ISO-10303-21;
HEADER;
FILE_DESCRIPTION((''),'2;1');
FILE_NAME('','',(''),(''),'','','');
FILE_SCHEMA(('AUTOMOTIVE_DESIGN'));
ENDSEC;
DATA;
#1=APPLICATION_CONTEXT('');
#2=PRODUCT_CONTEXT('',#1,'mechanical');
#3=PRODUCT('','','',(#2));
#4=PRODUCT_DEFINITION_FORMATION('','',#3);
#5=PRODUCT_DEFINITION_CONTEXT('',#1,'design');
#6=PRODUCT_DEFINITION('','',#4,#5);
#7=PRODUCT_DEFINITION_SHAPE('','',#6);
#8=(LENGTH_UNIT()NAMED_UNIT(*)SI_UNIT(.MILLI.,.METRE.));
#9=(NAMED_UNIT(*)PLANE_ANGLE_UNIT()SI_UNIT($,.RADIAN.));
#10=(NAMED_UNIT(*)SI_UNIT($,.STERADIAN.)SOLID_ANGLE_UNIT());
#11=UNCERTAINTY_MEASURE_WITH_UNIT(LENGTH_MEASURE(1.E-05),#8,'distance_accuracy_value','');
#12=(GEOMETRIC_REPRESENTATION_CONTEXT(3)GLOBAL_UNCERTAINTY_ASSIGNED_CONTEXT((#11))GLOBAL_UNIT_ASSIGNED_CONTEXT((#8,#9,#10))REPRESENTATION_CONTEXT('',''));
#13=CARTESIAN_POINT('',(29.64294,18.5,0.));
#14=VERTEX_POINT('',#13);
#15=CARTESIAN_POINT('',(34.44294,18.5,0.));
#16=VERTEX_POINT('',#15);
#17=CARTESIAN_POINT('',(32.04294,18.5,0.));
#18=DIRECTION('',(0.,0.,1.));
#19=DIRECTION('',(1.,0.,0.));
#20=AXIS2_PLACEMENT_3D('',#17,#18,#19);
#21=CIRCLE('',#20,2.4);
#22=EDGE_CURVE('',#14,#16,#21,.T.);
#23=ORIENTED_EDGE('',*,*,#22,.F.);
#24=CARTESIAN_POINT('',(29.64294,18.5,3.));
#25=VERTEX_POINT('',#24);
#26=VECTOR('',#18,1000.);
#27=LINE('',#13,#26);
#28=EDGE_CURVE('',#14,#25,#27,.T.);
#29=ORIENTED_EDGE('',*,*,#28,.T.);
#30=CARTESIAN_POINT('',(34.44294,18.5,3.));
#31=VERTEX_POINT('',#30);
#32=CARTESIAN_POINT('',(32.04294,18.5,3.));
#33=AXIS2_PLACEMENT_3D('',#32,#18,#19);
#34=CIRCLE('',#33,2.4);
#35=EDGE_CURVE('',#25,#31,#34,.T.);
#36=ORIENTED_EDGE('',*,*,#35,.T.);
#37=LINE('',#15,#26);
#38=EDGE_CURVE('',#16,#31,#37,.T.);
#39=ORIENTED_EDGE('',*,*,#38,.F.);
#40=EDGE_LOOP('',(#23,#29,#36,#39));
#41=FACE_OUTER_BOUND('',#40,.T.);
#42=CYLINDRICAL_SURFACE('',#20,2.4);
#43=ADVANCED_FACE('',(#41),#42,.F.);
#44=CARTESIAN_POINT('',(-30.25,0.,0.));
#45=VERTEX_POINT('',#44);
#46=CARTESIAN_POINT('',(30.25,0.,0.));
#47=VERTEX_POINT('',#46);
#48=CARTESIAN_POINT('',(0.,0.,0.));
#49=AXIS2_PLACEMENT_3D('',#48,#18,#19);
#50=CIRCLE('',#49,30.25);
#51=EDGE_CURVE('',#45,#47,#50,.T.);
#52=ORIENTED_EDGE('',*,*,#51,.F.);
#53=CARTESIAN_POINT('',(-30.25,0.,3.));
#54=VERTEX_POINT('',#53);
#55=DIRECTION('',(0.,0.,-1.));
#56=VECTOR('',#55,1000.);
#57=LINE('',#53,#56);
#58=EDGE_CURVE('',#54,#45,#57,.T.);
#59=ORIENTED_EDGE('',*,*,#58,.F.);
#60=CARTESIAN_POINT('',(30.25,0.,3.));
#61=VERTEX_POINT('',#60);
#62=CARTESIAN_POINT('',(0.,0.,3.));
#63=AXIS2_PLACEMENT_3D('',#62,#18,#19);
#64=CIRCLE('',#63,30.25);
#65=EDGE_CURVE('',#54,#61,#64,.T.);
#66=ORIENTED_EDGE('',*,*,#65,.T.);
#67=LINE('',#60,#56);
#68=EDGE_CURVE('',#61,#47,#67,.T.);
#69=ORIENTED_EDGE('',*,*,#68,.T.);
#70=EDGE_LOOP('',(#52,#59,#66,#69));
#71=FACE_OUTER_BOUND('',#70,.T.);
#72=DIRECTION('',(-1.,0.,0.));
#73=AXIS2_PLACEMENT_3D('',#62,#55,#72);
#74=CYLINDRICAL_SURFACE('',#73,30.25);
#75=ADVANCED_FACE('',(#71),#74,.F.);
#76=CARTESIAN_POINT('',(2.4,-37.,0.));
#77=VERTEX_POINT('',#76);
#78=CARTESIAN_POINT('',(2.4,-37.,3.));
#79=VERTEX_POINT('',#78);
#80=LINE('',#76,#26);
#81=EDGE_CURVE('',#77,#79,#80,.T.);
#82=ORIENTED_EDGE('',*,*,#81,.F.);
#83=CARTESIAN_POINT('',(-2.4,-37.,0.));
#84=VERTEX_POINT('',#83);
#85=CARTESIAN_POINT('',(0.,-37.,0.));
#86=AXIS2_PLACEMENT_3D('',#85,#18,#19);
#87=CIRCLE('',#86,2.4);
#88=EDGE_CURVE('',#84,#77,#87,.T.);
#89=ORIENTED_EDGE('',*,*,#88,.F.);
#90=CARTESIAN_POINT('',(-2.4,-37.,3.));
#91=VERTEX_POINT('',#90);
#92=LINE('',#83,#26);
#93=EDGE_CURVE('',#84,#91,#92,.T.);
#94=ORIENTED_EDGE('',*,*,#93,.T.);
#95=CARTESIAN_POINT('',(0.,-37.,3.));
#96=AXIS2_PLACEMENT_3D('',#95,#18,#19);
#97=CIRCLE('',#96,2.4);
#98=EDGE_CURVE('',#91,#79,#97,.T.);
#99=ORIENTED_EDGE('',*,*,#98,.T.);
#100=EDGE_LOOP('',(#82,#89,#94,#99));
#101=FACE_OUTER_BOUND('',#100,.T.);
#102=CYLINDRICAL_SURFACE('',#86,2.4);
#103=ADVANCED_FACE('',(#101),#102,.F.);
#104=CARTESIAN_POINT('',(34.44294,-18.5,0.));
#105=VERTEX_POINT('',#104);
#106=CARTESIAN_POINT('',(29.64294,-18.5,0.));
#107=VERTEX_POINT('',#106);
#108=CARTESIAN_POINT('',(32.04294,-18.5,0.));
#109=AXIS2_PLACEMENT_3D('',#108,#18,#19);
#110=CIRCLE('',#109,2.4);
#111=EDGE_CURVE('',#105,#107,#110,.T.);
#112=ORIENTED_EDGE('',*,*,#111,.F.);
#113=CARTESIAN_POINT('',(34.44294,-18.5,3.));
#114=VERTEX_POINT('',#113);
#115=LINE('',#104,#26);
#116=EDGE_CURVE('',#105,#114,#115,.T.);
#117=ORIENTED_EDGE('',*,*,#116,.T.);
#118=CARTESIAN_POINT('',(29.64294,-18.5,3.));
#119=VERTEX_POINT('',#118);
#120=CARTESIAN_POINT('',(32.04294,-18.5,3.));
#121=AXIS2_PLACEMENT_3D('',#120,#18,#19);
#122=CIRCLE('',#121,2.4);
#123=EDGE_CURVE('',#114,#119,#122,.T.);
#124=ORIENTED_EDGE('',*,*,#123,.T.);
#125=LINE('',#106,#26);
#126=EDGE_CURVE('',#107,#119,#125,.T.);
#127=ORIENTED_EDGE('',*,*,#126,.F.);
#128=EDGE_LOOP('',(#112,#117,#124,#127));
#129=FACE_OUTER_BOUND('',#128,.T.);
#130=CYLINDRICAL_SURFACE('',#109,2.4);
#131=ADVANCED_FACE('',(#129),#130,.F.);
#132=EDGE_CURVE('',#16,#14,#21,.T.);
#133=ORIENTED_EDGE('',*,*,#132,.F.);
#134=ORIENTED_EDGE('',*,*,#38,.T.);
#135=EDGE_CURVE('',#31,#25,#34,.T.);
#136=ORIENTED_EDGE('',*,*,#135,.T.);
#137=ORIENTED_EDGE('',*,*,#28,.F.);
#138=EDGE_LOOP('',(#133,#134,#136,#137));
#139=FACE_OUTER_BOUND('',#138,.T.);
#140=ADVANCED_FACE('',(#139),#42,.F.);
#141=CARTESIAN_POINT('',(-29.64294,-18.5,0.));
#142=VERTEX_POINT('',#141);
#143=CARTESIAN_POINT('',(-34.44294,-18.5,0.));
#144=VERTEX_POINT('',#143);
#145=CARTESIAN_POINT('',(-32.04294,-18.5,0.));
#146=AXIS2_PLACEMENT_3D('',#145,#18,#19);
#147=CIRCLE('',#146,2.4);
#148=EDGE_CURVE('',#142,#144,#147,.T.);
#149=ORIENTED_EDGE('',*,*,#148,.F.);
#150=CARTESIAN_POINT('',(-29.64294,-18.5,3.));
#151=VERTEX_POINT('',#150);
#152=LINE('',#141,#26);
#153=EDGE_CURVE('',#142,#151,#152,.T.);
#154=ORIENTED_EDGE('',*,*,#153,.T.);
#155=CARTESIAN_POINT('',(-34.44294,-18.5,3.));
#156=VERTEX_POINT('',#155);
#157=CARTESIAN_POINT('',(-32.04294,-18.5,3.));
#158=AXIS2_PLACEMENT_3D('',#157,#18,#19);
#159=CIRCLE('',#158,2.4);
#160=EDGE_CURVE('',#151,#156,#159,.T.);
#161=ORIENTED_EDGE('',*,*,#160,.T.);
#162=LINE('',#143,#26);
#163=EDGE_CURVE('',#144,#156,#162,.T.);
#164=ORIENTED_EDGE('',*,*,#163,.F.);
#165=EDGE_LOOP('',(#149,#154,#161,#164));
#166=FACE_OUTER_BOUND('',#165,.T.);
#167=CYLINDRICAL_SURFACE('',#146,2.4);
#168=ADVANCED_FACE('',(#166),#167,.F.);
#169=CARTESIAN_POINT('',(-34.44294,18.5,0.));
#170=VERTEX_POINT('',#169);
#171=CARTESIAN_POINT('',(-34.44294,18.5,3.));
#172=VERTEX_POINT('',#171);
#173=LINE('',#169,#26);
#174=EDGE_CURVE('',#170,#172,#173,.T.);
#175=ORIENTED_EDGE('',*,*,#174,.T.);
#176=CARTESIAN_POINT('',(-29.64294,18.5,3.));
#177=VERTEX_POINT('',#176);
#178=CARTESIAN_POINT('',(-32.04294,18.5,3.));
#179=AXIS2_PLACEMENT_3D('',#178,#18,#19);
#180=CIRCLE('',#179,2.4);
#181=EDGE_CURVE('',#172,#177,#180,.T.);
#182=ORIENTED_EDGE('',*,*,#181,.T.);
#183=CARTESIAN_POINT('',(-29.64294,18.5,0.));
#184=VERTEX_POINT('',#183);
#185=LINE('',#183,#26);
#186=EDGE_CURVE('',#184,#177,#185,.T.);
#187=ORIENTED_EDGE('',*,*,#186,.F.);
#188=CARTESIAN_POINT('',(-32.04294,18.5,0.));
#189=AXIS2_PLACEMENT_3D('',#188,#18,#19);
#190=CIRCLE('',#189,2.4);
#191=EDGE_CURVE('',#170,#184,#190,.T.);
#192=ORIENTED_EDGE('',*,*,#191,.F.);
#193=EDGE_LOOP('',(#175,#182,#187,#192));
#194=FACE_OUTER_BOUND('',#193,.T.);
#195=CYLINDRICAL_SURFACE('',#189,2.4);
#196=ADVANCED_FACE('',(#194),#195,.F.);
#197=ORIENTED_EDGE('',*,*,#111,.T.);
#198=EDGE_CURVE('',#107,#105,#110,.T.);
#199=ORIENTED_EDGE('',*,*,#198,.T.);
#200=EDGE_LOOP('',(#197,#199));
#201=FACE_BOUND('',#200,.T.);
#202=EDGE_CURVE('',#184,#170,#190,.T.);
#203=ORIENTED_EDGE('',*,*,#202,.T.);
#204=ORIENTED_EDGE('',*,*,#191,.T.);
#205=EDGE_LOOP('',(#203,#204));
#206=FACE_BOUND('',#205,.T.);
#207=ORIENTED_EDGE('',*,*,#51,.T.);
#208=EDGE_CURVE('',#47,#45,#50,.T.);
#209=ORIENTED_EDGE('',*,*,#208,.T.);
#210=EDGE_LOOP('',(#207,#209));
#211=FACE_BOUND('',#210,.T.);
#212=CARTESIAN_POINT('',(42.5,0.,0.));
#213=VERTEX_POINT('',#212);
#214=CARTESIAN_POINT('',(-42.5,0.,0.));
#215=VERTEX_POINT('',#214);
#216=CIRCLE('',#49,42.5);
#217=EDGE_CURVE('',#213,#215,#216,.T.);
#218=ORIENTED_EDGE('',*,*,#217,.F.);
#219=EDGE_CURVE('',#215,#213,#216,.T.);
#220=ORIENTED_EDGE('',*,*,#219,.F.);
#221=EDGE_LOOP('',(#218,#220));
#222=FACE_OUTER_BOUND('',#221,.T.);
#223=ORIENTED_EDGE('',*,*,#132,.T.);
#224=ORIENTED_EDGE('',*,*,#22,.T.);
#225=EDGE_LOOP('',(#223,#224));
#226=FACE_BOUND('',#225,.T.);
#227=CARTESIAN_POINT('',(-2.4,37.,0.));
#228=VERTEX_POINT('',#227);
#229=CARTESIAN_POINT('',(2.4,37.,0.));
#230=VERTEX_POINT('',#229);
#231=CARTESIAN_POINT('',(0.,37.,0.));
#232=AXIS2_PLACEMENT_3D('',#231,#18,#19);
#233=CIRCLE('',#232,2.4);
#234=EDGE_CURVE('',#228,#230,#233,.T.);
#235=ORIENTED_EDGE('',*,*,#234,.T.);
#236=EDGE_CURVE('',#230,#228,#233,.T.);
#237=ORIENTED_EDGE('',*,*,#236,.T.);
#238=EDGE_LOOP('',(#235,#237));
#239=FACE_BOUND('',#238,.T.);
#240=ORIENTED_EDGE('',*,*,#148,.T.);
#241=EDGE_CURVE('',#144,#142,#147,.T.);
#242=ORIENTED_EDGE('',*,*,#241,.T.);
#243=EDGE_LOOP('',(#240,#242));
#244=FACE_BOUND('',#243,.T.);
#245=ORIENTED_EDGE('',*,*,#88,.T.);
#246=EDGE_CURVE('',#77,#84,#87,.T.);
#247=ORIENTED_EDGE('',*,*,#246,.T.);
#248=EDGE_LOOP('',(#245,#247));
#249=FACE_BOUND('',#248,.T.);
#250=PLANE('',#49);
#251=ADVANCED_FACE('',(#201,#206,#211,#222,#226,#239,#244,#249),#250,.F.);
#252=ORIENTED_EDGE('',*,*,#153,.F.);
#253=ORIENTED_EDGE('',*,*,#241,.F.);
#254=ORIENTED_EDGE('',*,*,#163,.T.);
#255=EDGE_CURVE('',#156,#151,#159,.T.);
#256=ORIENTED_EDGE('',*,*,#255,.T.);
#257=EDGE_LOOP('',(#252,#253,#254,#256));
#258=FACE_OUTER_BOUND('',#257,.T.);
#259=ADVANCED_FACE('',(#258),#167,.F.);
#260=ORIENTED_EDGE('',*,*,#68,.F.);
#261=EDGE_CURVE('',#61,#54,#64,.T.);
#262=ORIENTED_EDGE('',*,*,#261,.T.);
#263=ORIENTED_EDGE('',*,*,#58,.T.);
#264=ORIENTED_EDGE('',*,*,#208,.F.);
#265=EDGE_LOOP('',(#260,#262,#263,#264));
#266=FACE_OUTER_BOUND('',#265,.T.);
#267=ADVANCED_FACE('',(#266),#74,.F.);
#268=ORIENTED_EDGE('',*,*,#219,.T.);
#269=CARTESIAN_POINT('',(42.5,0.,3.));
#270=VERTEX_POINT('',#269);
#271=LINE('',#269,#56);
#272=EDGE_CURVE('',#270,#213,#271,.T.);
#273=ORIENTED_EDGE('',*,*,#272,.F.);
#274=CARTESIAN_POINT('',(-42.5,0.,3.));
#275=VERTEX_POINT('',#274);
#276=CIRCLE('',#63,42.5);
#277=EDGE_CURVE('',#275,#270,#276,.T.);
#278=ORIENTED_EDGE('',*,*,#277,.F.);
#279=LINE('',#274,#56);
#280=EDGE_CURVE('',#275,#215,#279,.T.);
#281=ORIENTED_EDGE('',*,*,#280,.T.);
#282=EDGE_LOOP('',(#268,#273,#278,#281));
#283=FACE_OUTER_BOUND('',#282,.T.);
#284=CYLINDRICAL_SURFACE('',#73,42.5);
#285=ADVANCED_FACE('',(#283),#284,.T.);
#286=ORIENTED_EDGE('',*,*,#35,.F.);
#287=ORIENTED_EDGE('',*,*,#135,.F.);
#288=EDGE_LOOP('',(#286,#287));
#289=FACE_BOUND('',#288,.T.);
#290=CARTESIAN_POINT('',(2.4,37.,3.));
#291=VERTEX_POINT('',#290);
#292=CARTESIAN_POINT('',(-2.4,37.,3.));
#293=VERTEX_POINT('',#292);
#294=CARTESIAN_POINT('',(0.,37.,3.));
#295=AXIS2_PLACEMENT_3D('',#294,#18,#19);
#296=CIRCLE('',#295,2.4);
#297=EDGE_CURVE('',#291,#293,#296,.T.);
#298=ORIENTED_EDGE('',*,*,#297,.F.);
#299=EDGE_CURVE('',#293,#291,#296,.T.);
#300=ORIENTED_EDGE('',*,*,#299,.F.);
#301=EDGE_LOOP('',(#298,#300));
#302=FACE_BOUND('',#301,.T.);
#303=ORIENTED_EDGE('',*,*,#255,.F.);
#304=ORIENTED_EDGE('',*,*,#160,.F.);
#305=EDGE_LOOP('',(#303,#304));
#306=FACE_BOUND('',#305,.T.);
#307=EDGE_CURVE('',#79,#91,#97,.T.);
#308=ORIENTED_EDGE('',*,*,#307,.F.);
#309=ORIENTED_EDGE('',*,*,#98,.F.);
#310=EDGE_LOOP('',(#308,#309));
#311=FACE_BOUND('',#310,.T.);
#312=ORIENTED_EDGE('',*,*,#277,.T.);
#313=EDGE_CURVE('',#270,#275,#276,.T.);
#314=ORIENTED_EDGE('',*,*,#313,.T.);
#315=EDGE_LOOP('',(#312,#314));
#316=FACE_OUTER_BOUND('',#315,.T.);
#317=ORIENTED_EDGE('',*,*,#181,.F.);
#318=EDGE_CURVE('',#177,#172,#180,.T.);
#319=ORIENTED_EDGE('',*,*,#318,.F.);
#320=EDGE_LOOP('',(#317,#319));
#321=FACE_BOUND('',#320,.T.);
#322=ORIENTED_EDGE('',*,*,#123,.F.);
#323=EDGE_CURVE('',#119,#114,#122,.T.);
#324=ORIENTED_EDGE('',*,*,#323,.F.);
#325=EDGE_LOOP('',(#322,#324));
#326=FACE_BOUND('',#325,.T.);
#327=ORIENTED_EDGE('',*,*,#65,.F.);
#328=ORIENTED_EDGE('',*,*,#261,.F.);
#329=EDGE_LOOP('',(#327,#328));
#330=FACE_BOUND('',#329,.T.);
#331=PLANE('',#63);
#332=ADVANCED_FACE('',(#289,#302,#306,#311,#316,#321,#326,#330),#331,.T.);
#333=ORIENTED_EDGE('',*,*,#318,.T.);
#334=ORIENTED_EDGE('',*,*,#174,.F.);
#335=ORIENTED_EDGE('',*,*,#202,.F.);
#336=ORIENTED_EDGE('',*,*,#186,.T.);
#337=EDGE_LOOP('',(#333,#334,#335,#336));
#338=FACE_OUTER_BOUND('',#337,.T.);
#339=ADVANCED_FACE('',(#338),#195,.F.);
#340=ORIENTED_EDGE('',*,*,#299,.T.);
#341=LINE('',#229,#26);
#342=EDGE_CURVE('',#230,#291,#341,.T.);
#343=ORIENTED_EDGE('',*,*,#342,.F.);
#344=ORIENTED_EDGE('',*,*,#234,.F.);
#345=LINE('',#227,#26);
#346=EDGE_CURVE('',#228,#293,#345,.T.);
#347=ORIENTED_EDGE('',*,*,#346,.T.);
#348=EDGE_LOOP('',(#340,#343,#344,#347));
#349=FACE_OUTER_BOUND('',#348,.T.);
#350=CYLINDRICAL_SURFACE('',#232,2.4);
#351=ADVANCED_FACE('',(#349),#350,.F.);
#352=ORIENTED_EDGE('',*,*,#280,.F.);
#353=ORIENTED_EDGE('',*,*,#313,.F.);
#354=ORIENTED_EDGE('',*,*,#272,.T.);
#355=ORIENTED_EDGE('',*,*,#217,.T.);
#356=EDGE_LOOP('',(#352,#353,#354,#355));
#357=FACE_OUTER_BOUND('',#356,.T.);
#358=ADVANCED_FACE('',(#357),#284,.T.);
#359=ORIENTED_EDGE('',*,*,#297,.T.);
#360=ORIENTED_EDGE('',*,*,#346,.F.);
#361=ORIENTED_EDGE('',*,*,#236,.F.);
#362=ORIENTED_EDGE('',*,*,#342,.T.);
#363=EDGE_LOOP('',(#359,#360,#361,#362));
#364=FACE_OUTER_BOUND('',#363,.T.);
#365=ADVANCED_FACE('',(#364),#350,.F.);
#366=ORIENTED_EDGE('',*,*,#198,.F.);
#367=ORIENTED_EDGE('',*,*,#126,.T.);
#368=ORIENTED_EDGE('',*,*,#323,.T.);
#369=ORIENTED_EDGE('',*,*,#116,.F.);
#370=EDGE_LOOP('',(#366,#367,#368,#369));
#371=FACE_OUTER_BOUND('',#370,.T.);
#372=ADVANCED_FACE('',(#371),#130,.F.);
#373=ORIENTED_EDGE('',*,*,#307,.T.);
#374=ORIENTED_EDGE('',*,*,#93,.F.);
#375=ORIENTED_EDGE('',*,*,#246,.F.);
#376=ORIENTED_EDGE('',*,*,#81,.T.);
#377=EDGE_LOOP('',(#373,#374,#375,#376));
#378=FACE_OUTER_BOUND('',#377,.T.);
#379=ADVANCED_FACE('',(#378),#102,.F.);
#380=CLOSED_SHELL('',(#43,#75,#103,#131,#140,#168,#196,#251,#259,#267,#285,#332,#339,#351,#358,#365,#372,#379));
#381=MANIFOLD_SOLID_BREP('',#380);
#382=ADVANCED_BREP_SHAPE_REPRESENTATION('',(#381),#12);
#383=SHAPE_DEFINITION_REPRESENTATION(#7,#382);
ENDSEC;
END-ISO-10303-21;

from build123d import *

# Parameters (mm, degrees)
SKETCH1_R           = 42.5
SKETCH1_R_2         = 30.25
BOSS_EXTRUDE1_DEPTH = 3
SKETCH2_R           = 2.4
CUT_EXTRUDE1_DEPTH  = 3


with BuildPart() as part:
    # Sketch1 → Boss-Extrude1 (new body)
    with BuildSketch(Plane.XY):
        Circle(SKETCH1_R)
        Circle(SKETCH1_R_2, mode=Mode.SUBTRACT)
    extrude(amount=BOSS_EXTRUDE1_DEPTH)

    # Sketch2 → Cut-Extrude1 (cut)
    with BuildSketch(Plane.XY.offset(3)):
        with Locations((0, 37)):
            Circle(SKETCH2_R)
        with Locations((32.04293994, 18.5)):
            Circle(SKETCH2_R)
        with Locations((32.04293994, -18.5)):
            Circle(SKETCH2_R)
        with Locations((0, -37)):
            Circle(SKETCH2_R)
        with Locations((-32.04293994, -18.5)):
            Circle(SKETCH2_R)
        with Locations((-32.04293994, 18.5)):
            Circle(SKETCH2_R)
    extrude(amount=-CUT_EXTRUDE1_DEPTH, mode=Mode.SUBTRACT)


solid = part.part
